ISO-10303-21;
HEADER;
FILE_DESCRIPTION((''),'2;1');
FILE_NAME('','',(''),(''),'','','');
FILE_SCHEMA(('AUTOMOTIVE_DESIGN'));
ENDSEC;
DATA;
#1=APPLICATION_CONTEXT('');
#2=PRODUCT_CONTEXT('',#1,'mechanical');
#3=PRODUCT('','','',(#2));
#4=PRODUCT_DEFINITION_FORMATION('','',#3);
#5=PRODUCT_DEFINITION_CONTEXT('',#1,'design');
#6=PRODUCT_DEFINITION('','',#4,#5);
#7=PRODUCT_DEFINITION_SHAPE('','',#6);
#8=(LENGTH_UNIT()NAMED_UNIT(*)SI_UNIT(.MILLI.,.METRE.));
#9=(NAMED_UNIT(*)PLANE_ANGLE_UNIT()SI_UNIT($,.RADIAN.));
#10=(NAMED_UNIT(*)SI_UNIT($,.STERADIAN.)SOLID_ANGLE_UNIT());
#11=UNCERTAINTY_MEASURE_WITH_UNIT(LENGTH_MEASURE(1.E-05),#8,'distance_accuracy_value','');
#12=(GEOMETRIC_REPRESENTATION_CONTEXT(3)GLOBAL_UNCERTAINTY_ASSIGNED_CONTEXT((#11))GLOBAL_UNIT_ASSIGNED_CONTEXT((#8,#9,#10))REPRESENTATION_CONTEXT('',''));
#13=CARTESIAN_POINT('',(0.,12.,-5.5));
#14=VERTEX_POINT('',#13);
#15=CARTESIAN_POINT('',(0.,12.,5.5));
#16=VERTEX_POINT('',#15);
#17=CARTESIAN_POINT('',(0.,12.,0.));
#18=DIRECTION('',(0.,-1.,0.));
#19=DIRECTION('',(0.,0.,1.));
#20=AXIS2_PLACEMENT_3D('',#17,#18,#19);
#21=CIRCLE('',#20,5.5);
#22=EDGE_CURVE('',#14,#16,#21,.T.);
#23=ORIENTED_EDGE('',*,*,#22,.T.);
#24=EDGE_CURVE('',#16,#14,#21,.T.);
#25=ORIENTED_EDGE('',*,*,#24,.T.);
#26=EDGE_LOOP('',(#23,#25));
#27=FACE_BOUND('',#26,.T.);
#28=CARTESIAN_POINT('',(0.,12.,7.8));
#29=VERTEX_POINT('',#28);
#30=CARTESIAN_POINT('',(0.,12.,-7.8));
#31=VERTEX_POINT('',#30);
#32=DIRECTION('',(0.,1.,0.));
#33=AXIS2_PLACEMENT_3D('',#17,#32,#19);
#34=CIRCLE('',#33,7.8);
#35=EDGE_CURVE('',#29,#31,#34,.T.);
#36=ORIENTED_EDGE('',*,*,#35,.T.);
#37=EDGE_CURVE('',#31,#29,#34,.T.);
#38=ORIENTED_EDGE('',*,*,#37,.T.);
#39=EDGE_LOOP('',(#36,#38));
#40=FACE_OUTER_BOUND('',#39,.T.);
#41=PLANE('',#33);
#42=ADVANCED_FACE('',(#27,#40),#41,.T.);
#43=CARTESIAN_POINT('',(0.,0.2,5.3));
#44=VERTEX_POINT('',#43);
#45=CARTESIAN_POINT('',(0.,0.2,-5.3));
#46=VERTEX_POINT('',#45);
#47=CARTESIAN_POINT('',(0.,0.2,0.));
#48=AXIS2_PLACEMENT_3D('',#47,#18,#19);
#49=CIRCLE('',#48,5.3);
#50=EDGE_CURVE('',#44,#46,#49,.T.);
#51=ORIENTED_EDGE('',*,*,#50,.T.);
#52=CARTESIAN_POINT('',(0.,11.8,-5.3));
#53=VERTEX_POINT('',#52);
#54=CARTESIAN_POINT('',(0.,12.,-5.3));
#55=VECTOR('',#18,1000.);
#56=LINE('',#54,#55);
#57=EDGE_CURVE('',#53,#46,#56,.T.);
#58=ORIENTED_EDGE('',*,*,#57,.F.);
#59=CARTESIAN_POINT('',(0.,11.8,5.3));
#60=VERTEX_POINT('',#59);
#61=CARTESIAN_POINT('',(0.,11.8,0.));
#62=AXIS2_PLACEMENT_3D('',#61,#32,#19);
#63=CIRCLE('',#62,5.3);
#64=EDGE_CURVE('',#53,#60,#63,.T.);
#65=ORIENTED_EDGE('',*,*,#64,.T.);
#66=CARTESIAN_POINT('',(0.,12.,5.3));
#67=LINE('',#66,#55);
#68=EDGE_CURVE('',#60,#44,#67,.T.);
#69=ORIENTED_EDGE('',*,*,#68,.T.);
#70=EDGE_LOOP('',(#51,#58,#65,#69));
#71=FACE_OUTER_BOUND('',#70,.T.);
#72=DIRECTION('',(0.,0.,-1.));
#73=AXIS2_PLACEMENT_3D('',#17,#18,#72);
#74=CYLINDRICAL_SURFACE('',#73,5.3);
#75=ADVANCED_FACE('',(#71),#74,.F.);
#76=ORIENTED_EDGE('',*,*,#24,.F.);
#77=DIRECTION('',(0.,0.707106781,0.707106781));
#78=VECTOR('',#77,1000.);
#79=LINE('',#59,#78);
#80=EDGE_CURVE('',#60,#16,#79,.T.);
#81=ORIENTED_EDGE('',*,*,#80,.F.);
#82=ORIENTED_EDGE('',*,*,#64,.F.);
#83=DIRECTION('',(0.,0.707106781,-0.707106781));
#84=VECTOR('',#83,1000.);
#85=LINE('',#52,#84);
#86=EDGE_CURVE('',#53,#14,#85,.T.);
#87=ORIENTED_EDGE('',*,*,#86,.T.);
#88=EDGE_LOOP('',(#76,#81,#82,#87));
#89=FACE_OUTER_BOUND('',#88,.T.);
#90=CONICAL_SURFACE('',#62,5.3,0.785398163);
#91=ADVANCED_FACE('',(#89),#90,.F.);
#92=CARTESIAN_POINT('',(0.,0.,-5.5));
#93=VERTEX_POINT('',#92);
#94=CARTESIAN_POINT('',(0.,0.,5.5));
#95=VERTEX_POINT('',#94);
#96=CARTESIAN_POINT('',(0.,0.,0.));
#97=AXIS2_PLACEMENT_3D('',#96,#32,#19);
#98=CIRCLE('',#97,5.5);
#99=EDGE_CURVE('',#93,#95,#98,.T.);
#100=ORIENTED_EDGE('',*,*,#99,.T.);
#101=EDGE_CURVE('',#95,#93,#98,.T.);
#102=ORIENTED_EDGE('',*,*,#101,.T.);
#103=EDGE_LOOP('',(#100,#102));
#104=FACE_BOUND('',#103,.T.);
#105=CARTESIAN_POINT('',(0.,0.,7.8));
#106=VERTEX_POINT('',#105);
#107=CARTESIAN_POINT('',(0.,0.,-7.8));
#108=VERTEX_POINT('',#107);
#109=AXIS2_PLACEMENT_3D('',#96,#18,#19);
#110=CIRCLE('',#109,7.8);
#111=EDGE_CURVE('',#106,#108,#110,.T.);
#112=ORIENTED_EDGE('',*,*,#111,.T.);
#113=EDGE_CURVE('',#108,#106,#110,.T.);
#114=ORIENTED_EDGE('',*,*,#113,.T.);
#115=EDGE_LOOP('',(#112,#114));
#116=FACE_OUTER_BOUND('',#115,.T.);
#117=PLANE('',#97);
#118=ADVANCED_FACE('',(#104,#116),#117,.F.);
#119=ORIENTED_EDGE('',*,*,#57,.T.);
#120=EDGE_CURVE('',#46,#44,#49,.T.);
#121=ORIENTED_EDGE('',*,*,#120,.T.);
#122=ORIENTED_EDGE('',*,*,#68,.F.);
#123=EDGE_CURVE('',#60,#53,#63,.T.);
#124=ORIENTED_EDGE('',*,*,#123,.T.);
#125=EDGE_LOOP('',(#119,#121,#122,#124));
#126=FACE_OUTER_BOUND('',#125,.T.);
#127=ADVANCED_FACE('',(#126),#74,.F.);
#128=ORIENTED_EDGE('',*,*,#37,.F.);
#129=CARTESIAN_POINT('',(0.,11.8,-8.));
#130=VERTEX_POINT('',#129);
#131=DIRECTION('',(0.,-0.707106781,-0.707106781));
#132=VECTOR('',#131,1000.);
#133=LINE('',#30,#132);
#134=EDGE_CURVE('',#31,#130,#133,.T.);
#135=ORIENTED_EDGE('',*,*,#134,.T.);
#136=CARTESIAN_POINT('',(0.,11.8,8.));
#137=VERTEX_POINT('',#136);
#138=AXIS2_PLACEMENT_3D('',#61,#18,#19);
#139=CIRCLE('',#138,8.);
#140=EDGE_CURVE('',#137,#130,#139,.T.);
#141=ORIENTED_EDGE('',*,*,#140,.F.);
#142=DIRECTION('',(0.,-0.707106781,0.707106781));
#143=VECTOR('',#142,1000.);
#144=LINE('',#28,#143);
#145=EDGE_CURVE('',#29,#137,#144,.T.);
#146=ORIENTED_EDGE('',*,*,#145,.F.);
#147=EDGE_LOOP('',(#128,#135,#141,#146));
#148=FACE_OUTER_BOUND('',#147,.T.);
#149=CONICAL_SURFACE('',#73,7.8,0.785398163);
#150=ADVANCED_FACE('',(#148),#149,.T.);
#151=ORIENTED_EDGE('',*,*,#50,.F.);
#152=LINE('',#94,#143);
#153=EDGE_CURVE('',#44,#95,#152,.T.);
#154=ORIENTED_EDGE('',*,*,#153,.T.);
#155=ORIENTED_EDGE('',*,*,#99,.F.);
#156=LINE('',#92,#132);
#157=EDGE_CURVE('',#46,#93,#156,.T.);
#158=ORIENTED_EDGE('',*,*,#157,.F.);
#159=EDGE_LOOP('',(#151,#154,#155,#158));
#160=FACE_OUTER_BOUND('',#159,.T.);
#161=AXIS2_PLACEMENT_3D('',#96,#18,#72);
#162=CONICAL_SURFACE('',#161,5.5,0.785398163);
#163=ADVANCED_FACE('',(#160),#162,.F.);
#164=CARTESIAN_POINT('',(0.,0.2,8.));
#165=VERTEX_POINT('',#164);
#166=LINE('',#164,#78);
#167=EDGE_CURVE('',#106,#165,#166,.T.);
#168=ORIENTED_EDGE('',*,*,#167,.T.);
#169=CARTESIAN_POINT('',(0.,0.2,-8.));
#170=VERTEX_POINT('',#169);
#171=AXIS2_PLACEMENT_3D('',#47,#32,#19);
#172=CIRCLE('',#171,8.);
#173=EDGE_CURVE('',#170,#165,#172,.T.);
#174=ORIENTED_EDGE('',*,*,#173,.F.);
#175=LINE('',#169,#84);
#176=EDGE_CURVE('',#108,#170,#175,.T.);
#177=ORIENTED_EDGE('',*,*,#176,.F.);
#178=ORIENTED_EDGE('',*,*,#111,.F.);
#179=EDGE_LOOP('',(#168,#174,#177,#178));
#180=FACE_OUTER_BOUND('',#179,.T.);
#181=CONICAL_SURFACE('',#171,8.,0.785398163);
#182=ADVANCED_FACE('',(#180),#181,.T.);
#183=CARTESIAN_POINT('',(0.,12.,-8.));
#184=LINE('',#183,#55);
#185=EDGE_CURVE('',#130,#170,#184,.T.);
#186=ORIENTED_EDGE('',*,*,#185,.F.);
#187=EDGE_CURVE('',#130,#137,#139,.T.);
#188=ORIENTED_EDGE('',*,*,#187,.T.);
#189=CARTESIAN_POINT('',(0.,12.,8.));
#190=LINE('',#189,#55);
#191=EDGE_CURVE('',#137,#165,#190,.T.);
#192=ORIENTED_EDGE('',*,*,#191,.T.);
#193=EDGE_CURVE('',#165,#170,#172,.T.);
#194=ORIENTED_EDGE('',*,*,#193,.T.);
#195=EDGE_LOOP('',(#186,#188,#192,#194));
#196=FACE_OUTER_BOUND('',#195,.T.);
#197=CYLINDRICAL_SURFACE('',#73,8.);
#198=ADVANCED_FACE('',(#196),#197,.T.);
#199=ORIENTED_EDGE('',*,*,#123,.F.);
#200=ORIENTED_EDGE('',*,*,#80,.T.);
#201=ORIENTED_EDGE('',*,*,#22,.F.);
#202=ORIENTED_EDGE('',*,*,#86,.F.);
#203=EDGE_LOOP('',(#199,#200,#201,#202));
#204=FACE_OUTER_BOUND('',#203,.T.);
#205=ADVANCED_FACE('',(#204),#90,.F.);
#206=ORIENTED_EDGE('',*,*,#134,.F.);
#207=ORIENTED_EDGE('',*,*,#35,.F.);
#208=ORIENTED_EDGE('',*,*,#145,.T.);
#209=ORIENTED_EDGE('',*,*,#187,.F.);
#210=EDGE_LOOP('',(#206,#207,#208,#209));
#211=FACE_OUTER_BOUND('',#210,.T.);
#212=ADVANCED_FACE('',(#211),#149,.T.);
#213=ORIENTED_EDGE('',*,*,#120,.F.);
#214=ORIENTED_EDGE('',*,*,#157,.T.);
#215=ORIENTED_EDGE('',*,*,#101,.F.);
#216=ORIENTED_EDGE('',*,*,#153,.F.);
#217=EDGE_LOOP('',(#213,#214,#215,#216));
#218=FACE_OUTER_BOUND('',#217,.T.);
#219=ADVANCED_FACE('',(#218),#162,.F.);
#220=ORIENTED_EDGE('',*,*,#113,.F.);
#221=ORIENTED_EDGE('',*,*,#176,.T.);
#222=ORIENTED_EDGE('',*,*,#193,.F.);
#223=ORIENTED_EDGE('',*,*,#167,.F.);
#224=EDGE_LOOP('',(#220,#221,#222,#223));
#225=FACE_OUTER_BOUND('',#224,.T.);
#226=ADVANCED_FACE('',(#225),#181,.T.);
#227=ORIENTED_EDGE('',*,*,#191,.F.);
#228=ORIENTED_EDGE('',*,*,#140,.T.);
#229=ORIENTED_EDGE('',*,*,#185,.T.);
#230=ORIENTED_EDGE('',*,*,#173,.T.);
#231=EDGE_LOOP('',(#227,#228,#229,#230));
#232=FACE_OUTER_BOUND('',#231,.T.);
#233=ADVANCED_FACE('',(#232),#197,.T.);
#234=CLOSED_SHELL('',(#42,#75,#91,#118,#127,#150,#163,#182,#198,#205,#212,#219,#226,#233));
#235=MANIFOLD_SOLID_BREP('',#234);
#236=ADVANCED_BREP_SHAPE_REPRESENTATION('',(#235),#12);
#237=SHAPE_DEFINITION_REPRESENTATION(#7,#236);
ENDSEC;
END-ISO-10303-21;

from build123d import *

# Parameters (mm, degrees)
SKETCH1_R           = 8
SKETCH1_R_2         = 5.3
BOSS_EXTRUDE1_DEPTH = 12
CHAMFER1_SIZE       = 0.2


with BuildPart() as part:
    # Sketch1 → Boss-Extrude1 (new body)
    with BuildSketch(Plane(origin=(0, 0, 0), x_dir=(1, 0, 0), z_dir=(0, 1, 0))):
        with Locations(Location((0, 0, 0), (0, 0, 270))):
            Circle(SKETCH1_R)
        with Locations(Location((0, 0, 0), (0, 0, 270))):
            Circle(SKETCH1_R_2, mode=Mode.SUBTRACT)
    extrude(amount=BOSS_EXTRUDE1_DEPTH)

    # Chamfer1
    chamfer1_edges = [part.edges().sort_by_distance(p)[0] for p in [
        (0, 0, -8),
        (0, 12, -8),
        (0, 0, -5.3),
        (0, 12, -5.3),
    ]]
    chamfer(chamfer1_edges, length=CHAMFER1_SIZE)


solid = part.part
